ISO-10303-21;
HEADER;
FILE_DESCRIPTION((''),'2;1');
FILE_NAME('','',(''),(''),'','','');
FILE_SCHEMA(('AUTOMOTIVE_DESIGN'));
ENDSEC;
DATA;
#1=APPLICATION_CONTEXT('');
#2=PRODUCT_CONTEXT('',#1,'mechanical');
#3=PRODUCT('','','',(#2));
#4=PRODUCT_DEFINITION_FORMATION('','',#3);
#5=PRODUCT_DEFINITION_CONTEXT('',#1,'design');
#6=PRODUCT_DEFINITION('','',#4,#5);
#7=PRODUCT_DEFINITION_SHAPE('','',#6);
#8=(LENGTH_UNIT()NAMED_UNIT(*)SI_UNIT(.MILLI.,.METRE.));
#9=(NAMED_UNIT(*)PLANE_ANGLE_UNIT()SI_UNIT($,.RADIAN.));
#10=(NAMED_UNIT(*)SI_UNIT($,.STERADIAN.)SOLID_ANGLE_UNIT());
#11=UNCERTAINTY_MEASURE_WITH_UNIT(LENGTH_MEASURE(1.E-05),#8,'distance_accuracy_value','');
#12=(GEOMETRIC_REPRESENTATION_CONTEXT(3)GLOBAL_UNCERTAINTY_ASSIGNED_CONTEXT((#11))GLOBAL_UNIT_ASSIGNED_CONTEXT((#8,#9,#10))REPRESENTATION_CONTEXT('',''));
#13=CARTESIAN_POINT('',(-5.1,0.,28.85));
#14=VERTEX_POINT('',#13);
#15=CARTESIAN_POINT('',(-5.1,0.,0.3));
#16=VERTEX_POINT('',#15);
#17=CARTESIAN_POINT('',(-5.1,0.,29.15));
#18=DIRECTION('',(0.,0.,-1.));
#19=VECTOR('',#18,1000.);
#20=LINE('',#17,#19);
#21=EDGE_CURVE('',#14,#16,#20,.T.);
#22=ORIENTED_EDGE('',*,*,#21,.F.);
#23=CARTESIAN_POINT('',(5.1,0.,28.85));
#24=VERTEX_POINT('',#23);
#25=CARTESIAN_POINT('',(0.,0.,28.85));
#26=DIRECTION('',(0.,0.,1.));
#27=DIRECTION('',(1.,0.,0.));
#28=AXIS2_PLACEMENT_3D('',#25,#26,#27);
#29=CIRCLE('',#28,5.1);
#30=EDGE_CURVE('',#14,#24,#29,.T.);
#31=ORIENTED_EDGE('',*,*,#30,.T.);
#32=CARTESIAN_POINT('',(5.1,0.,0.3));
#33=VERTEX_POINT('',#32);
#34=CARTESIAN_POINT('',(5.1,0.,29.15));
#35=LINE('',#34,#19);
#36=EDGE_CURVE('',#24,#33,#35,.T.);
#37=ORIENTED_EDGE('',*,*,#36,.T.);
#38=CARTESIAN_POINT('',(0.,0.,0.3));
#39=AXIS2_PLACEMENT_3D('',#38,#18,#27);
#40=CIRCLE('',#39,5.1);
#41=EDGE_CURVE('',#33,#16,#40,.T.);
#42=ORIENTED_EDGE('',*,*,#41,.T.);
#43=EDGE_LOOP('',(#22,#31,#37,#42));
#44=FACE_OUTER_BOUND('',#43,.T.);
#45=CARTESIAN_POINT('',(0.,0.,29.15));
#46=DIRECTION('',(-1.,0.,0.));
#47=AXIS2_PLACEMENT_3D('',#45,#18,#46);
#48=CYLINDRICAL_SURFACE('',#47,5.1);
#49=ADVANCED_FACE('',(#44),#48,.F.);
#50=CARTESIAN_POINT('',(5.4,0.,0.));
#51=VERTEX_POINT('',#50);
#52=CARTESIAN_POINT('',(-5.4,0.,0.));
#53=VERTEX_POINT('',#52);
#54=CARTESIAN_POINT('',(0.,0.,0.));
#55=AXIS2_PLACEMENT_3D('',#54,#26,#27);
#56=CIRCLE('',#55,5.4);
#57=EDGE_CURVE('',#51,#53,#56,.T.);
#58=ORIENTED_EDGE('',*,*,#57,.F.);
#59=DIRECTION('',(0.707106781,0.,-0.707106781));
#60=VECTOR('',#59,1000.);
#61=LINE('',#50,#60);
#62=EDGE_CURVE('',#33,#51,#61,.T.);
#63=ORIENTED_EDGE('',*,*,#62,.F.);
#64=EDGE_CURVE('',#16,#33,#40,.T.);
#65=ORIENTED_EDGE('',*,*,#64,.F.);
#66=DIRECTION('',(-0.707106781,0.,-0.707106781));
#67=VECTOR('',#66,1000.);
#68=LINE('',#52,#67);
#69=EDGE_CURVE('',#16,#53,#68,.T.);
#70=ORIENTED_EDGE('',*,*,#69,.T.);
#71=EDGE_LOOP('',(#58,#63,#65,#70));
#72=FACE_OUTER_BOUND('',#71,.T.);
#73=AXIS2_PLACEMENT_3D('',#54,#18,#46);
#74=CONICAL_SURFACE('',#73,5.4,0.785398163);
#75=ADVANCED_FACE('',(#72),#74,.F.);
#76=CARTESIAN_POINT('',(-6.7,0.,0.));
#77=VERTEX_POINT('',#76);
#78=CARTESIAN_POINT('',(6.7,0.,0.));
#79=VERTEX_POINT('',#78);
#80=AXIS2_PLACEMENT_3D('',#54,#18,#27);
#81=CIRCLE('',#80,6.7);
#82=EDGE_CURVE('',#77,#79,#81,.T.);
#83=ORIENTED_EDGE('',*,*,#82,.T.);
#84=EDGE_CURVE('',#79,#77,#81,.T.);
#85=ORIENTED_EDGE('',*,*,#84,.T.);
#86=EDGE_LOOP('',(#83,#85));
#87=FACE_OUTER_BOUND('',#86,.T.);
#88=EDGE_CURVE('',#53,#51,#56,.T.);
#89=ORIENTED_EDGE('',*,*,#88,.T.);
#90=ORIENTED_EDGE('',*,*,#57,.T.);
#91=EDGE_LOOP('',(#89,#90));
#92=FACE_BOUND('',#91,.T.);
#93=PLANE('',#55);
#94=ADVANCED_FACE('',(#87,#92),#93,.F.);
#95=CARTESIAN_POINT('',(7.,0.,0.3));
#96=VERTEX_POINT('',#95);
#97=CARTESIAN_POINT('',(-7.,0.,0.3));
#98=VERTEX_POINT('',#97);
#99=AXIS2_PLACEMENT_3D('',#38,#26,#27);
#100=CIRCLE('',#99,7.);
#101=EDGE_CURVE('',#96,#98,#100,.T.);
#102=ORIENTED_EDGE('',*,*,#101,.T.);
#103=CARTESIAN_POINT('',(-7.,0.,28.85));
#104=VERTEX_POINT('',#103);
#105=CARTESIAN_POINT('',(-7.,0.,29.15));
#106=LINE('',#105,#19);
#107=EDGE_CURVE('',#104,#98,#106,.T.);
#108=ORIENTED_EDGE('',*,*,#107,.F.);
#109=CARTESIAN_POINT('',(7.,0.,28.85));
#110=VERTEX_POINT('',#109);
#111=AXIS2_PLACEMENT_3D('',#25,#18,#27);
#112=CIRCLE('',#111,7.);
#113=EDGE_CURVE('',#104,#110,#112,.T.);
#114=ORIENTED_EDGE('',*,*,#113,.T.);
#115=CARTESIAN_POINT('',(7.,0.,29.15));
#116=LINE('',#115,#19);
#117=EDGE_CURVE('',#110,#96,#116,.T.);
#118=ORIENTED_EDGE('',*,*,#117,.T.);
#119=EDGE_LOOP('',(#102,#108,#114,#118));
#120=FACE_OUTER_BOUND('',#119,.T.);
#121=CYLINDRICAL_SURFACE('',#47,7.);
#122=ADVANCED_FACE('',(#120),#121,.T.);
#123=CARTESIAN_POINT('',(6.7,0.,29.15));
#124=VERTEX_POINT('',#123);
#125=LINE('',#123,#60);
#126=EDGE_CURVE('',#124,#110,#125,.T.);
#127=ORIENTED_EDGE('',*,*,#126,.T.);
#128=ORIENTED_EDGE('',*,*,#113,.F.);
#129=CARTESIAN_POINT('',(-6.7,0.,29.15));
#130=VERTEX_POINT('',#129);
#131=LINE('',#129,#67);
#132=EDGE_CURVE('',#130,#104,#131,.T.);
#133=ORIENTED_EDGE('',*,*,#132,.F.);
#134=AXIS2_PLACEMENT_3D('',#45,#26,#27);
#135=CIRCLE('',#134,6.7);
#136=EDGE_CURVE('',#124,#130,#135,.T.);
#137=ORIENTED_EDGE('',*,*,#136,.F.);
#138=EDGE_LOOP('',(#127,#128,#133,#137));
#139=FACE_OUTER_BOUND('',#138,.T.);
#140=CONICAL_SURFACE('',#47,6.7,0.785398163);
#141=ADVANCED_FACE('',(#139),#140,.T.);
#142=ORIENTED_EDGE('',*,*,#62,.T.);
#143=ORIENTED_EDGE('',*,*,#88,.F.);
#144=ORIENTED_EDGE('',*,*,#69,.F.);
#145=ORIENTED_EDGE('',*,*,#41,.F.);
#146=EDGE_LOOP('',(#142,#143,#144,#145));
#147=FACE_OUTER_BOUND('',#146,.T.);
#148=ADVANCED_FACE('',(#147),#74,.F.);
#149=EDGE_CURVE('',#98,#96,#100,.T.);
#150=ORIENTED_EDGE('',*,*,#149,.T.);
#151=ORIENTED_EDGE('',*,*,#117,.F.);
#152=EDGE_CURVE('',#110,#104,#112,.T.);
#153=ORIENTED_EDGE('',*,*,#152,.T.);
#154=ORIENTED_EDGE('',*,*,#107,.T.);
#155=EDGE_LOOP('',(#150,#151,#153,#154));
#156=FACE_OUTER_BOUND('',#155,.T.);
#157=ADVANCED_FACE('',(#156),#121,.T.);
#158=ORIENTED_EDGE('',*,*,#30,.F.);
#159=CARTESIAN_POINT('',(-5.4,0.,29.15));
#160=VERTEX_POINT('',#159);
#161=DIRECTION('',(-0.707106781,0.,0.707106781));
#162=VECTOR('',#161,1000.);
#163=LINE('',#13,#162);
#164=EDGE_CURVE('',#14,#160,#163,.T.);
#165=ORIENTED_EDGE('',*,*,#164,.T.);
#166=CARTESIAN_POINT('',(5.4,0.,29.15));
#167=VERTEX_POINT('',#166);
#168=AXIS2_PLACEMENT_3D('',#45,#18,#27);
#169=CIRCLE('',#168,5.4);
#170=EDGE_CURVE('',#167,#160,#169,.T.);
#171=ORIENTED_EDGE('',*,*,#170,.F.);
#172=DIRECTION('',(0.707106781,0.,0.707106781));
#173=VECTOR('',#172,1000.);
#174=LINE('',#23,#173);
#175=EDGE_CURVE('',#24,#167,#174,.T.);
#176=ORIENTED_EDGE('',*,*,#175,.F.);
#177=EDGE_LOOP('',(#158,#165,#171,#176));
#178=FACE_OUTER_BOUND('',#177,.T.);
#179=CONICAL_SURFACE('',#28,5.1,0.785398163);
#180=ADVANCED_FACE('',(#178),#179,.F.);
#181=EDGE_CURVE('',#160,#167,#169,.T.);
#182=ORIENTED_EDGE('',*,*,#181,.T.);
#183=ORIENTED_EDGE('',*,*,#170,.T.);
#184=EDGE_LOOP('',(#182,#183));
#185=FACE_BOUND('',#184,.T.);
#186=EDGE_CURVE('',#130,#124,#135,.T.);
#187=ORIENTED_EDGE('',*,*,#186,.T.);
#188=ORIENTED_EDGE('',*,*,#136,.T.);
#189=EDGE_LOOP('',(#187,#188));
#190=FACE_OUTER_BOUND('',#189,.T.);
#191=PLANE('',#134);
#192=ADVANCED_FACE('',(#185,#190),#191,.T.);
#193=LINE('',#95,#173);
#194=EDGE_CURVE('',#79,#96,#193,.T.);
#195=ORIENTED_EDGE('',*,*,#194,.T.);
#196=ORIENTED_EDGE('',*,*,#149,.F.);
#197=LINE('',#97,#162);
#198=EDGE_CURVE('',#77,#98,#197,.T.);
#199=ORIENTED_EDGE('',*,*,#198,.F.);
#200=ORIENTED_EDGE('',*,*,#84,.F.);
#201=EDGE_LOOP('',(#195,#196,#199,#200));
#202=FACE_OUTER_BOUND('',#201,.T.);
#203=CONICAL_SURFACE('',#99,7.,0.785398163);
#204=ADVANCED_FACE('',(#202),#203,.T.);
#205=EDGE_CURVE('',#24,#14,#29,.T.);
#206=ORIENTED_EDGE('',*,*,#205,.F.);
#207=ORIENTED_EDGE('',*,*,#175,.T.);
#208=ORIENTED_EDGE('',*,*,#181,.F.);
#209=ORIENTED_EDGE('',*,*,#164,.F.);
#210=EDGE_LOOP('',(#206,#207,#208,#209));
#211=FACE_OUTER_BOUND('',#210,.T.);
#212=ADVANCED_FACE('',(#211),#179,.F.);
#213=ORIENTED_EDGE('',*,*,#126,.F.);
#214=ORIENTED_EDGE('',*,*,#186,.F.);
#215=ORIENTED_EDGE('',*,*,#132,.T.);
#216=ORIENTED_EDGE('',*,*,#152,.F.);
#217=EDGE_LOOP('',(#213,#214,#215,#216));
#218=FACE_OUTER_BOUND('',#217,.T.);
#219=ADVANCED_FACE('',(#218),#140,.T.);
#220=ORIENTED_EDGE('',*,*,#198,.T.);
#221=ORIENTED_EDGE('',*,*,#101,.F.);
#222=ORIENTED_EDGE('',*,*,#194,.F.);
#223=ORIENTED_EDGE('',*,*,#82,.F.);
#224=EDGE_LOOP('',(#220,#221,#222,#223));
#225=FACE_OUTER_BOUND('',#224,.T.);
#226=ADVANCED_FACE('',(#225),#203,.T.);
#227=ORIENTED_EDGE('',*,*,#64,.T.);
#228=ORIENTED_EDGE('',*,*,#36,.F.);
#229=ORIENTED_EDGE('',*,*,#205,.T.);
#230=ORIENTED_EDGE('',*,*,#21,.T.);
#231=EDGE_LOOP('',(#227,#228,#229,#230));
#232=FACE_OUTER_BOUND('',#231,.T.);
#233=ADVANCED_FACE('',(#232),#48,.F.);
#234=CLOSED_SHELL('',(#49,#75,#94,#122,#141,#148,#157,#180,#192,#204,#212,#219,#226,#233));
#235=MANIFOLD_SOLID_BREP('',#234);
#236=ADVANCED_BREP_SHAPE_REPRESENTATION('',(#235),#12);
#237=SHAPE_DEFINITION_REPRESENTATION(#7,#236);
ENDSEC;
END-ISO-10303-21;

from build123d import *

# Parameters (mm, degrees)
SKETCH_1_R      = 7
SKETCH_1_R_2    = 5.1
EXTRUDE_1_DEPTH = 29.15
CHAMFER_1_SIZE  = 0.3
CHAMFER_2_SIZE  = 0.3


with BuildPart() as part:
    # 草图1 → 凸台-拉伸1 (new body)
    with BuildSketch(Plane.XY):
        Circle(SKETCH_1_R)
        Circle(SKETCH_1_R_2, mode=Mode.SUBTRACT)
    extrude(amount=EXTRUDE_1_DEPTH)

    # 倒角1
    chamfer_1_edges = [part.edges().sort_by_distance(p)[0] for p in [
        (-7, 0, 0),
    ]]
    chamfer(chamfer_1_edges, length=CHAMFER_1_SIZE)

    # 倒角2
    chamfer_2_edges = [part.edges().sort_by_distance(p)[0] for p in [
        (-7, 0, 29.15),
        (-5.1, 0, 0),
        (-5.1, 0, 29.15),
    ]]
    chamfer(chamfer_2_edges, length=CHAMFER_2_SIZE)


solid = part.part
